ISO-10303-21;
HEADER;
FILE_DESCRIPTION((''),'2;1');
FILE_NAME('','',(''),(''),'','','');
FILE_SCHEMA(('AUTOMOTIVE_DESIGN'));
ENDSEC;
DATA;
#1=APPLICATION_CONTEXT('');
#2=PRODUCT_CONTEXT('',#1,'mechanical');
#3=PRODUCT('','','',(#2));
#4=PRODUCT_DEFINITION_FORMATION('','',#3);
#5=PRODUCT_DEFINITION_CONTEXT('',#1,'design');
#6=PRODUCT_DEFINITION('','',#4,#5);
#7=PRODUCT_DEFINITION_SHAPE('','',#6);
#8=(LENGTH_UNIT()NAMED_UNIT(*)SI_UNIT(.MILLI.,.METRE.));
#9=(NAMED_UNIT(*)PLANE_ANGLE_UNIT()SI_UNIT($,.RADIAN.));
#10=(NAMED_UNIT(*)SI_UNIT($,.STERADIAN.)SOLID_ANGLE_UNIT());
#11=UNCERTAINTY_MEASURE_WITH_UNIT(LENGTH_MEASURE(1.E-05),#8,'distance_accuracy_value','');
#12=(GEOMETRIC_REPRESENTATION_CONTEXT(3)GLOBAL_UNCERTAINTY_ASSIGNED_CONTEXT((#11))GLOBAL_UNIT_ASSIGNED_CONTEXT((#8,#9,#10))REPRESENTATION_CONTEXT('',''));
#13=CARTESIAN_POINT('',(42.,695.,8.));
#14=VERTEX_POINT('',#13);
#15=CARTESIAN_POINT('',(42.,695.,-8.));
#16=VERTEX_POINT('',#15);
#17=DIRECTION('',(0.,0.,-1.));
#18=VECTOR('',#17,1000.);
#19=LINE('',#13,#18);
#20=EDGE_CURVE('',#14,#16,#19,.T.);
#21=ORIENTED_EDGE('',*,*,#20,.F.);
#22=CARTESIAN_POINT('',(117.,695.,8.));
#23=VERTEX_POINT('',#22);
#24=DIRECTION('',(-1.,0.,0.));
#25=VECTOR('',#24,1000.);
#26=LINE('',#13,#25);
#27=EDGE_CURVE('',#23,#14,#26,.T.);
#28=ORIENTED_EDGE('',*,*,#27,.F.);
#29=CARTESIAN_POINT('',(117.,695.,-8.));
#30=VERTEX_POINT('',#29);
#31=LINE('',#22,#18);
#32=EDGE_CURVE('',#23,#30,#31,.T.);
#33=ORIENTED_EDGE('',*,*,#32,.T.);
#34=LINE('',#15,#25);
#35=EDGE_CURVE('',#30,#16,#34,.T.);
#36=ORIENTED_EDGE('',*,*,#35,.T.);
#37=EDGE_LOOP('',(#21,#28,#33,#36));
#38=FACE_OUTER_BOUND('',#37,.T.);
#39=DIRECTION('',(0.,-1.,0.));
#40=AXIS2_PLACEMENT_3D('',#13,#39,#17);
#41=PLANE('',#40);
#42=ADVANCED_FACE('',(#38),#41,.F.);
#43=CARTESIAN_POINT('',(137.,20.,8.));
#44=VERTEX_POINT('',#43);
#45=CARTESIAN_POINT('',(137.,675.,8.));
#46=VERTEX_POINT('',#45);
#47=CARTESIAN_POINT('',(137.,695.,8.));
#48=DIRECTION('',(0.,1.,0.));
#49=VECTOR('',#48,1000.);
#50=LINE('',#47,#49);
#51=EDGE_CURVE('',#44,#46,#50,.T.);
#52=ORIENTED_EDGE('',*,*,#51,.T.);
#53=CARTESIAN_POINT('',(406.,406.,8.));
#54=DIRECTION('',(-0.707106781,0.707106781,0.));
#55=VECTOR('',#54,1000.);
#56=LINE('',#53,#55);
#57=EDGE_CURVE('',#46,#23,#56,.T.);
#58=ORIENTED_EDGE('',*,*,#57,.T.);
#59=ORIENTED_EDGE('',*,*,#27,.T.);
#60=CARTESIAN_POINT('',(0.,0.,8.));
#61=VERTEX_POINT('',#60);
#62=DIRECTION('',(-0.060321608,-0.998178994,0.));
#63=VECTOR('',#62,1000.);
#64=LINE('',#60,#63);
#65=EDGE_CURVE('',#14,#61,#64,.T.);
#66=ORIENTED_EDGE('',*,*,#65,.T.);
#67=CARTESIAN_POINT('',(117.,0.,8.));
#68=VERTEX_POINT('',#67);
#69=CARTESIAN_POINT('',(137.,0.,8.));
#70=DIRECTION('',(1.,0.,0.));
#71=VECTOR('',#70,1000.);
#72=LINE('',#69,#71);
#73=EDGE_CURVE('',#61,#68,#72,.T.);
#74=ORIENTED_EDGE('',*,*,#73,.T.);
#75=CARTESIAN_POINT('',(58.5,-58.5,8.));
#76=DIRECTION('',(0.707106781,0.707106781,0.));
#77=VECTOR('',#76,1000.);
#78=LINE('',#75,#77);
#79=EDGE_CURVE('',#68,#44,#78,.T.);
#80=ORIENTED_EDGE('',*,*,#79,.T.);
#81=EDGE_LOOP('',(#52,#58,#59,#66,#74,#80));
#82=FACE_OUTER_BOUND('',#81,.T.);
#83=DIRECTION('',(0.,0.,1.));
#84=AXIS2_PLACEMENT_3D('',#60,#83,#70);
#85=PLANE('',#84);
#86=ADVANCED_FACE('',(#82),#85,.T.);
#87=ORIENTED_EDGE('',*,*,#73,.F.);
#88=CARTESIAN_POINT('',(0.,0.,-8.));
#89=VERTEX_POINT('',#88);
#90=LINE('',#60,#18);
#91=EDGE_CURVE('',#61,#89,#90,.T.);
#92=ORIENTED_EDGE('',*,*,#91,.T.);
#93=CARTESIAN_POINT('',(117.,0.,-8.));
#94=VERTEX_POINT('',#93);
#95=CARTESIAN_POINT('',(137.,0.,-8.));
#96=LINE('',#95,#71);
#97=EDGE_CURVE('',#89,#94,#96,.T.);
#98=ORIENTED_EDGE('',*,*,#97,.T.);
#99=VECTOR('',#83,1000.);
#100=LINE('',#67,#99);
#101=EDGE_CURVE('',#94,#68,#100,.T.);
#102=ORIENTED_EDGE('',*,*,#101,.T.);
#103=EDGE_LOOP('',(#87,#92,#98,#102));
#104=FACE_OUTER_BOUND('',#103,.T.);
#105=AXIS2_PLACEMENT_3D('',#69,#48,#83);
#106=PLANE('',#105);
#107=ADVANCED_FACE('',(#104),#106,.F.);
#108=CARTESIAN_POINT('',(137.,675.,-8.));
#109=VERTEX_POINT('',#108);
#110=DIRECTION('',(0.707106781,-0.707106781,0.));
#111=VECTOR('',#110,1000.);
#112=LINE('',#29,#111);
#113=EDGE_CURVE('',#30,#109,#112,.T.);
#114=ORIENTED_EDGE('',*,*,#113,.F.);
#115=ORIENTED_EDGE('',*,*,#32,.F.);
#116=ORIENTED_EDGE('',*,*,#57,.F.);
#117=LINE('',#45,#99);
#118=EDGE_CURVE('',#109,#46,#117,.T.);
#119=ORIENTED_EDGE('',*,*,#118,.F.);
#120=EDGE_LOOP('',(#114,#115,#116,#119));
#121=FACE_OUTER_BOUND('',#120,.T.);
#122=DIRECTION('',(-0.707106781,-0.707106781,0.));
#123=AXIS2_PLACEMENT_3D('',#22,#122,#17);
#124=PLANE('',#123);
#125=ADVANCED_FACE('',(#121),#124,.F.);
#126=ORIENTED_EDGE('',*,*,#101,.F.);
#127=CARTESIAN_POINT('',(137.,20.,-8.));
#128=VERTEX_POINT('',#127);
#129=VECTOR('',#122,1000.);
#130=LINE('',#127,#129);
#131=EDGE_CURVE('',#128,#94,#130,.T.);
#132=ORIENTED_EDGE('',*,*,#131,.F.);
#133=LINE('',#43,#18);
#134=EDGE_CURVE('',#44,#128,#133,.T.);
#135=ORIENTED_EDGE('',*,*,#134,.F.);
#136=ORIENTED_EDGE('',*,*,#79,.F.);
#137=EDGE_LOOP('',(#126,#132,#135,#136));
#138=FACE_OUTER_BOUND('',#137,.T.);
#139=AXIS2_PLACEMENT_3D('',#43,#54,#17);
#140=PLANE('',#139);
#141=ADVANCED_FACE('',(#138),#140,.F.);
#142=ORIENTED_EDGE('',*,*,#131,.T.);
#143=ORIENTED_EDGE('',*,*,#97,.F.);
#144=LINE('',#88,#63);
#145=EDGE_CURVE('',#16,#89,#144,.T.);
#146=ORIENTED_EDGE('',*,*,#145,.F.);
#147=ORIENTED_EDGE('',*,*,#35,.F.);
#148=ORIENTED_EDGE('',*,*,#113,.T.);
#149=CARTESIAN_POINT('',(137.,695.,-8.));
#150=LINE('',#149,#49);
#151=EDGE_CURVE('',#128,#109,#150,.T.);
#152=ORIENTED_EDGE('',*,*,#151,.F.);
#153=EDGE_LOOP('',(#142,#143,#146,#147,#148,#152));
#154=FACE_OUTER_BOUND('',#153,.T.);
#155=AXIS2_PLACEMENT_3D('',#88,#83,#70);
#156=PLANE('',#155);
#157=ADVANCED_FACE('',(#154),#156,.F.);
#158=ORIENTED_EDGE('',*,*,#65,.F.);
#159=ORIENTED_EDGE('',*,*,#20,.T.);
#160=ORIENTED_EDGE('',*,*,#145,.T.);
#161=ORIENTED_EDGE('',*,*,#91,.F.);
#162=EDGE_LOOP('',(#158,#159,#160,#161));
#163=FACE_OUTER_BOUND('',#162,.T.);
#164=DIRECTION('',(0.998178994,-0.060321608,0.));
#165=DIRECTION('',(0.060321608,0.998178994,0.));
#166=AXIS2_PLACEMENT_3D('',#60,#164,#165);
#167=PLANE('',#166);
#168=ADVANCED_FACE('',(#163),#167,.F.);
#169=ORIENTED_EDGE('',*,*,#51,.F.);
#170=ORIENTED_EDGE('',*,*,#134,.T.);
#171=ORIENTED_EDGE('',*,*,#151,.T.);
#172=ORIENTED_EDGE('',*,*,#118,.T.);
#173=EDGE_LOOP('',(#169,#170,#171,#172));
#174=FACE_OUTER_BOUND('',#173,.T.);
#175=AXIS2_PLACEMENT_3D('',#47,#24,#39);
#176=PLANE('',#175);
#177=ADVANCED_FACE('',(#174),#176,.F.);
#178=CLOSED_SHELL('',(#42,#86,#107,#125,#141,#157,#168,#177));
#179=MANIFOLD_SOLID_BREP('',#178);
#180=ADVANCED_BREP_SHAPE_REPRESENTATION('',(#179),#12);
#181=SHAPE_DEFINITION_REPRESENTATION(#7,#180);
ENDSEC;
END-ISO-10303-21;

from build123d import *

# Parameters (mm, degrees)
EXTRUDE_1_DEPTH = 8
CHAMFER_1_SIZE  = 20


with BuildPart() as part:
    # 草图2 → 凸台-拉伸1 (new, symmetric)
    with BuildSketch(Plane.XY):
        Polygon((0, 0), (42, 695), (137, 695), (137, 0), align=None)
    extrude(amount=EXTRUDE_1_DEPTH, both=True)

    # 倒角1
    chamfer_1_edges = [part.edges().sort_by_distance(p)[0] for p in [
        (137, 695, 0),
        (137, 0, 0),
    ]]
    chamfer(chamfer_1_edges, length=CHAMFER_1_SIZE)


solid = part.part
